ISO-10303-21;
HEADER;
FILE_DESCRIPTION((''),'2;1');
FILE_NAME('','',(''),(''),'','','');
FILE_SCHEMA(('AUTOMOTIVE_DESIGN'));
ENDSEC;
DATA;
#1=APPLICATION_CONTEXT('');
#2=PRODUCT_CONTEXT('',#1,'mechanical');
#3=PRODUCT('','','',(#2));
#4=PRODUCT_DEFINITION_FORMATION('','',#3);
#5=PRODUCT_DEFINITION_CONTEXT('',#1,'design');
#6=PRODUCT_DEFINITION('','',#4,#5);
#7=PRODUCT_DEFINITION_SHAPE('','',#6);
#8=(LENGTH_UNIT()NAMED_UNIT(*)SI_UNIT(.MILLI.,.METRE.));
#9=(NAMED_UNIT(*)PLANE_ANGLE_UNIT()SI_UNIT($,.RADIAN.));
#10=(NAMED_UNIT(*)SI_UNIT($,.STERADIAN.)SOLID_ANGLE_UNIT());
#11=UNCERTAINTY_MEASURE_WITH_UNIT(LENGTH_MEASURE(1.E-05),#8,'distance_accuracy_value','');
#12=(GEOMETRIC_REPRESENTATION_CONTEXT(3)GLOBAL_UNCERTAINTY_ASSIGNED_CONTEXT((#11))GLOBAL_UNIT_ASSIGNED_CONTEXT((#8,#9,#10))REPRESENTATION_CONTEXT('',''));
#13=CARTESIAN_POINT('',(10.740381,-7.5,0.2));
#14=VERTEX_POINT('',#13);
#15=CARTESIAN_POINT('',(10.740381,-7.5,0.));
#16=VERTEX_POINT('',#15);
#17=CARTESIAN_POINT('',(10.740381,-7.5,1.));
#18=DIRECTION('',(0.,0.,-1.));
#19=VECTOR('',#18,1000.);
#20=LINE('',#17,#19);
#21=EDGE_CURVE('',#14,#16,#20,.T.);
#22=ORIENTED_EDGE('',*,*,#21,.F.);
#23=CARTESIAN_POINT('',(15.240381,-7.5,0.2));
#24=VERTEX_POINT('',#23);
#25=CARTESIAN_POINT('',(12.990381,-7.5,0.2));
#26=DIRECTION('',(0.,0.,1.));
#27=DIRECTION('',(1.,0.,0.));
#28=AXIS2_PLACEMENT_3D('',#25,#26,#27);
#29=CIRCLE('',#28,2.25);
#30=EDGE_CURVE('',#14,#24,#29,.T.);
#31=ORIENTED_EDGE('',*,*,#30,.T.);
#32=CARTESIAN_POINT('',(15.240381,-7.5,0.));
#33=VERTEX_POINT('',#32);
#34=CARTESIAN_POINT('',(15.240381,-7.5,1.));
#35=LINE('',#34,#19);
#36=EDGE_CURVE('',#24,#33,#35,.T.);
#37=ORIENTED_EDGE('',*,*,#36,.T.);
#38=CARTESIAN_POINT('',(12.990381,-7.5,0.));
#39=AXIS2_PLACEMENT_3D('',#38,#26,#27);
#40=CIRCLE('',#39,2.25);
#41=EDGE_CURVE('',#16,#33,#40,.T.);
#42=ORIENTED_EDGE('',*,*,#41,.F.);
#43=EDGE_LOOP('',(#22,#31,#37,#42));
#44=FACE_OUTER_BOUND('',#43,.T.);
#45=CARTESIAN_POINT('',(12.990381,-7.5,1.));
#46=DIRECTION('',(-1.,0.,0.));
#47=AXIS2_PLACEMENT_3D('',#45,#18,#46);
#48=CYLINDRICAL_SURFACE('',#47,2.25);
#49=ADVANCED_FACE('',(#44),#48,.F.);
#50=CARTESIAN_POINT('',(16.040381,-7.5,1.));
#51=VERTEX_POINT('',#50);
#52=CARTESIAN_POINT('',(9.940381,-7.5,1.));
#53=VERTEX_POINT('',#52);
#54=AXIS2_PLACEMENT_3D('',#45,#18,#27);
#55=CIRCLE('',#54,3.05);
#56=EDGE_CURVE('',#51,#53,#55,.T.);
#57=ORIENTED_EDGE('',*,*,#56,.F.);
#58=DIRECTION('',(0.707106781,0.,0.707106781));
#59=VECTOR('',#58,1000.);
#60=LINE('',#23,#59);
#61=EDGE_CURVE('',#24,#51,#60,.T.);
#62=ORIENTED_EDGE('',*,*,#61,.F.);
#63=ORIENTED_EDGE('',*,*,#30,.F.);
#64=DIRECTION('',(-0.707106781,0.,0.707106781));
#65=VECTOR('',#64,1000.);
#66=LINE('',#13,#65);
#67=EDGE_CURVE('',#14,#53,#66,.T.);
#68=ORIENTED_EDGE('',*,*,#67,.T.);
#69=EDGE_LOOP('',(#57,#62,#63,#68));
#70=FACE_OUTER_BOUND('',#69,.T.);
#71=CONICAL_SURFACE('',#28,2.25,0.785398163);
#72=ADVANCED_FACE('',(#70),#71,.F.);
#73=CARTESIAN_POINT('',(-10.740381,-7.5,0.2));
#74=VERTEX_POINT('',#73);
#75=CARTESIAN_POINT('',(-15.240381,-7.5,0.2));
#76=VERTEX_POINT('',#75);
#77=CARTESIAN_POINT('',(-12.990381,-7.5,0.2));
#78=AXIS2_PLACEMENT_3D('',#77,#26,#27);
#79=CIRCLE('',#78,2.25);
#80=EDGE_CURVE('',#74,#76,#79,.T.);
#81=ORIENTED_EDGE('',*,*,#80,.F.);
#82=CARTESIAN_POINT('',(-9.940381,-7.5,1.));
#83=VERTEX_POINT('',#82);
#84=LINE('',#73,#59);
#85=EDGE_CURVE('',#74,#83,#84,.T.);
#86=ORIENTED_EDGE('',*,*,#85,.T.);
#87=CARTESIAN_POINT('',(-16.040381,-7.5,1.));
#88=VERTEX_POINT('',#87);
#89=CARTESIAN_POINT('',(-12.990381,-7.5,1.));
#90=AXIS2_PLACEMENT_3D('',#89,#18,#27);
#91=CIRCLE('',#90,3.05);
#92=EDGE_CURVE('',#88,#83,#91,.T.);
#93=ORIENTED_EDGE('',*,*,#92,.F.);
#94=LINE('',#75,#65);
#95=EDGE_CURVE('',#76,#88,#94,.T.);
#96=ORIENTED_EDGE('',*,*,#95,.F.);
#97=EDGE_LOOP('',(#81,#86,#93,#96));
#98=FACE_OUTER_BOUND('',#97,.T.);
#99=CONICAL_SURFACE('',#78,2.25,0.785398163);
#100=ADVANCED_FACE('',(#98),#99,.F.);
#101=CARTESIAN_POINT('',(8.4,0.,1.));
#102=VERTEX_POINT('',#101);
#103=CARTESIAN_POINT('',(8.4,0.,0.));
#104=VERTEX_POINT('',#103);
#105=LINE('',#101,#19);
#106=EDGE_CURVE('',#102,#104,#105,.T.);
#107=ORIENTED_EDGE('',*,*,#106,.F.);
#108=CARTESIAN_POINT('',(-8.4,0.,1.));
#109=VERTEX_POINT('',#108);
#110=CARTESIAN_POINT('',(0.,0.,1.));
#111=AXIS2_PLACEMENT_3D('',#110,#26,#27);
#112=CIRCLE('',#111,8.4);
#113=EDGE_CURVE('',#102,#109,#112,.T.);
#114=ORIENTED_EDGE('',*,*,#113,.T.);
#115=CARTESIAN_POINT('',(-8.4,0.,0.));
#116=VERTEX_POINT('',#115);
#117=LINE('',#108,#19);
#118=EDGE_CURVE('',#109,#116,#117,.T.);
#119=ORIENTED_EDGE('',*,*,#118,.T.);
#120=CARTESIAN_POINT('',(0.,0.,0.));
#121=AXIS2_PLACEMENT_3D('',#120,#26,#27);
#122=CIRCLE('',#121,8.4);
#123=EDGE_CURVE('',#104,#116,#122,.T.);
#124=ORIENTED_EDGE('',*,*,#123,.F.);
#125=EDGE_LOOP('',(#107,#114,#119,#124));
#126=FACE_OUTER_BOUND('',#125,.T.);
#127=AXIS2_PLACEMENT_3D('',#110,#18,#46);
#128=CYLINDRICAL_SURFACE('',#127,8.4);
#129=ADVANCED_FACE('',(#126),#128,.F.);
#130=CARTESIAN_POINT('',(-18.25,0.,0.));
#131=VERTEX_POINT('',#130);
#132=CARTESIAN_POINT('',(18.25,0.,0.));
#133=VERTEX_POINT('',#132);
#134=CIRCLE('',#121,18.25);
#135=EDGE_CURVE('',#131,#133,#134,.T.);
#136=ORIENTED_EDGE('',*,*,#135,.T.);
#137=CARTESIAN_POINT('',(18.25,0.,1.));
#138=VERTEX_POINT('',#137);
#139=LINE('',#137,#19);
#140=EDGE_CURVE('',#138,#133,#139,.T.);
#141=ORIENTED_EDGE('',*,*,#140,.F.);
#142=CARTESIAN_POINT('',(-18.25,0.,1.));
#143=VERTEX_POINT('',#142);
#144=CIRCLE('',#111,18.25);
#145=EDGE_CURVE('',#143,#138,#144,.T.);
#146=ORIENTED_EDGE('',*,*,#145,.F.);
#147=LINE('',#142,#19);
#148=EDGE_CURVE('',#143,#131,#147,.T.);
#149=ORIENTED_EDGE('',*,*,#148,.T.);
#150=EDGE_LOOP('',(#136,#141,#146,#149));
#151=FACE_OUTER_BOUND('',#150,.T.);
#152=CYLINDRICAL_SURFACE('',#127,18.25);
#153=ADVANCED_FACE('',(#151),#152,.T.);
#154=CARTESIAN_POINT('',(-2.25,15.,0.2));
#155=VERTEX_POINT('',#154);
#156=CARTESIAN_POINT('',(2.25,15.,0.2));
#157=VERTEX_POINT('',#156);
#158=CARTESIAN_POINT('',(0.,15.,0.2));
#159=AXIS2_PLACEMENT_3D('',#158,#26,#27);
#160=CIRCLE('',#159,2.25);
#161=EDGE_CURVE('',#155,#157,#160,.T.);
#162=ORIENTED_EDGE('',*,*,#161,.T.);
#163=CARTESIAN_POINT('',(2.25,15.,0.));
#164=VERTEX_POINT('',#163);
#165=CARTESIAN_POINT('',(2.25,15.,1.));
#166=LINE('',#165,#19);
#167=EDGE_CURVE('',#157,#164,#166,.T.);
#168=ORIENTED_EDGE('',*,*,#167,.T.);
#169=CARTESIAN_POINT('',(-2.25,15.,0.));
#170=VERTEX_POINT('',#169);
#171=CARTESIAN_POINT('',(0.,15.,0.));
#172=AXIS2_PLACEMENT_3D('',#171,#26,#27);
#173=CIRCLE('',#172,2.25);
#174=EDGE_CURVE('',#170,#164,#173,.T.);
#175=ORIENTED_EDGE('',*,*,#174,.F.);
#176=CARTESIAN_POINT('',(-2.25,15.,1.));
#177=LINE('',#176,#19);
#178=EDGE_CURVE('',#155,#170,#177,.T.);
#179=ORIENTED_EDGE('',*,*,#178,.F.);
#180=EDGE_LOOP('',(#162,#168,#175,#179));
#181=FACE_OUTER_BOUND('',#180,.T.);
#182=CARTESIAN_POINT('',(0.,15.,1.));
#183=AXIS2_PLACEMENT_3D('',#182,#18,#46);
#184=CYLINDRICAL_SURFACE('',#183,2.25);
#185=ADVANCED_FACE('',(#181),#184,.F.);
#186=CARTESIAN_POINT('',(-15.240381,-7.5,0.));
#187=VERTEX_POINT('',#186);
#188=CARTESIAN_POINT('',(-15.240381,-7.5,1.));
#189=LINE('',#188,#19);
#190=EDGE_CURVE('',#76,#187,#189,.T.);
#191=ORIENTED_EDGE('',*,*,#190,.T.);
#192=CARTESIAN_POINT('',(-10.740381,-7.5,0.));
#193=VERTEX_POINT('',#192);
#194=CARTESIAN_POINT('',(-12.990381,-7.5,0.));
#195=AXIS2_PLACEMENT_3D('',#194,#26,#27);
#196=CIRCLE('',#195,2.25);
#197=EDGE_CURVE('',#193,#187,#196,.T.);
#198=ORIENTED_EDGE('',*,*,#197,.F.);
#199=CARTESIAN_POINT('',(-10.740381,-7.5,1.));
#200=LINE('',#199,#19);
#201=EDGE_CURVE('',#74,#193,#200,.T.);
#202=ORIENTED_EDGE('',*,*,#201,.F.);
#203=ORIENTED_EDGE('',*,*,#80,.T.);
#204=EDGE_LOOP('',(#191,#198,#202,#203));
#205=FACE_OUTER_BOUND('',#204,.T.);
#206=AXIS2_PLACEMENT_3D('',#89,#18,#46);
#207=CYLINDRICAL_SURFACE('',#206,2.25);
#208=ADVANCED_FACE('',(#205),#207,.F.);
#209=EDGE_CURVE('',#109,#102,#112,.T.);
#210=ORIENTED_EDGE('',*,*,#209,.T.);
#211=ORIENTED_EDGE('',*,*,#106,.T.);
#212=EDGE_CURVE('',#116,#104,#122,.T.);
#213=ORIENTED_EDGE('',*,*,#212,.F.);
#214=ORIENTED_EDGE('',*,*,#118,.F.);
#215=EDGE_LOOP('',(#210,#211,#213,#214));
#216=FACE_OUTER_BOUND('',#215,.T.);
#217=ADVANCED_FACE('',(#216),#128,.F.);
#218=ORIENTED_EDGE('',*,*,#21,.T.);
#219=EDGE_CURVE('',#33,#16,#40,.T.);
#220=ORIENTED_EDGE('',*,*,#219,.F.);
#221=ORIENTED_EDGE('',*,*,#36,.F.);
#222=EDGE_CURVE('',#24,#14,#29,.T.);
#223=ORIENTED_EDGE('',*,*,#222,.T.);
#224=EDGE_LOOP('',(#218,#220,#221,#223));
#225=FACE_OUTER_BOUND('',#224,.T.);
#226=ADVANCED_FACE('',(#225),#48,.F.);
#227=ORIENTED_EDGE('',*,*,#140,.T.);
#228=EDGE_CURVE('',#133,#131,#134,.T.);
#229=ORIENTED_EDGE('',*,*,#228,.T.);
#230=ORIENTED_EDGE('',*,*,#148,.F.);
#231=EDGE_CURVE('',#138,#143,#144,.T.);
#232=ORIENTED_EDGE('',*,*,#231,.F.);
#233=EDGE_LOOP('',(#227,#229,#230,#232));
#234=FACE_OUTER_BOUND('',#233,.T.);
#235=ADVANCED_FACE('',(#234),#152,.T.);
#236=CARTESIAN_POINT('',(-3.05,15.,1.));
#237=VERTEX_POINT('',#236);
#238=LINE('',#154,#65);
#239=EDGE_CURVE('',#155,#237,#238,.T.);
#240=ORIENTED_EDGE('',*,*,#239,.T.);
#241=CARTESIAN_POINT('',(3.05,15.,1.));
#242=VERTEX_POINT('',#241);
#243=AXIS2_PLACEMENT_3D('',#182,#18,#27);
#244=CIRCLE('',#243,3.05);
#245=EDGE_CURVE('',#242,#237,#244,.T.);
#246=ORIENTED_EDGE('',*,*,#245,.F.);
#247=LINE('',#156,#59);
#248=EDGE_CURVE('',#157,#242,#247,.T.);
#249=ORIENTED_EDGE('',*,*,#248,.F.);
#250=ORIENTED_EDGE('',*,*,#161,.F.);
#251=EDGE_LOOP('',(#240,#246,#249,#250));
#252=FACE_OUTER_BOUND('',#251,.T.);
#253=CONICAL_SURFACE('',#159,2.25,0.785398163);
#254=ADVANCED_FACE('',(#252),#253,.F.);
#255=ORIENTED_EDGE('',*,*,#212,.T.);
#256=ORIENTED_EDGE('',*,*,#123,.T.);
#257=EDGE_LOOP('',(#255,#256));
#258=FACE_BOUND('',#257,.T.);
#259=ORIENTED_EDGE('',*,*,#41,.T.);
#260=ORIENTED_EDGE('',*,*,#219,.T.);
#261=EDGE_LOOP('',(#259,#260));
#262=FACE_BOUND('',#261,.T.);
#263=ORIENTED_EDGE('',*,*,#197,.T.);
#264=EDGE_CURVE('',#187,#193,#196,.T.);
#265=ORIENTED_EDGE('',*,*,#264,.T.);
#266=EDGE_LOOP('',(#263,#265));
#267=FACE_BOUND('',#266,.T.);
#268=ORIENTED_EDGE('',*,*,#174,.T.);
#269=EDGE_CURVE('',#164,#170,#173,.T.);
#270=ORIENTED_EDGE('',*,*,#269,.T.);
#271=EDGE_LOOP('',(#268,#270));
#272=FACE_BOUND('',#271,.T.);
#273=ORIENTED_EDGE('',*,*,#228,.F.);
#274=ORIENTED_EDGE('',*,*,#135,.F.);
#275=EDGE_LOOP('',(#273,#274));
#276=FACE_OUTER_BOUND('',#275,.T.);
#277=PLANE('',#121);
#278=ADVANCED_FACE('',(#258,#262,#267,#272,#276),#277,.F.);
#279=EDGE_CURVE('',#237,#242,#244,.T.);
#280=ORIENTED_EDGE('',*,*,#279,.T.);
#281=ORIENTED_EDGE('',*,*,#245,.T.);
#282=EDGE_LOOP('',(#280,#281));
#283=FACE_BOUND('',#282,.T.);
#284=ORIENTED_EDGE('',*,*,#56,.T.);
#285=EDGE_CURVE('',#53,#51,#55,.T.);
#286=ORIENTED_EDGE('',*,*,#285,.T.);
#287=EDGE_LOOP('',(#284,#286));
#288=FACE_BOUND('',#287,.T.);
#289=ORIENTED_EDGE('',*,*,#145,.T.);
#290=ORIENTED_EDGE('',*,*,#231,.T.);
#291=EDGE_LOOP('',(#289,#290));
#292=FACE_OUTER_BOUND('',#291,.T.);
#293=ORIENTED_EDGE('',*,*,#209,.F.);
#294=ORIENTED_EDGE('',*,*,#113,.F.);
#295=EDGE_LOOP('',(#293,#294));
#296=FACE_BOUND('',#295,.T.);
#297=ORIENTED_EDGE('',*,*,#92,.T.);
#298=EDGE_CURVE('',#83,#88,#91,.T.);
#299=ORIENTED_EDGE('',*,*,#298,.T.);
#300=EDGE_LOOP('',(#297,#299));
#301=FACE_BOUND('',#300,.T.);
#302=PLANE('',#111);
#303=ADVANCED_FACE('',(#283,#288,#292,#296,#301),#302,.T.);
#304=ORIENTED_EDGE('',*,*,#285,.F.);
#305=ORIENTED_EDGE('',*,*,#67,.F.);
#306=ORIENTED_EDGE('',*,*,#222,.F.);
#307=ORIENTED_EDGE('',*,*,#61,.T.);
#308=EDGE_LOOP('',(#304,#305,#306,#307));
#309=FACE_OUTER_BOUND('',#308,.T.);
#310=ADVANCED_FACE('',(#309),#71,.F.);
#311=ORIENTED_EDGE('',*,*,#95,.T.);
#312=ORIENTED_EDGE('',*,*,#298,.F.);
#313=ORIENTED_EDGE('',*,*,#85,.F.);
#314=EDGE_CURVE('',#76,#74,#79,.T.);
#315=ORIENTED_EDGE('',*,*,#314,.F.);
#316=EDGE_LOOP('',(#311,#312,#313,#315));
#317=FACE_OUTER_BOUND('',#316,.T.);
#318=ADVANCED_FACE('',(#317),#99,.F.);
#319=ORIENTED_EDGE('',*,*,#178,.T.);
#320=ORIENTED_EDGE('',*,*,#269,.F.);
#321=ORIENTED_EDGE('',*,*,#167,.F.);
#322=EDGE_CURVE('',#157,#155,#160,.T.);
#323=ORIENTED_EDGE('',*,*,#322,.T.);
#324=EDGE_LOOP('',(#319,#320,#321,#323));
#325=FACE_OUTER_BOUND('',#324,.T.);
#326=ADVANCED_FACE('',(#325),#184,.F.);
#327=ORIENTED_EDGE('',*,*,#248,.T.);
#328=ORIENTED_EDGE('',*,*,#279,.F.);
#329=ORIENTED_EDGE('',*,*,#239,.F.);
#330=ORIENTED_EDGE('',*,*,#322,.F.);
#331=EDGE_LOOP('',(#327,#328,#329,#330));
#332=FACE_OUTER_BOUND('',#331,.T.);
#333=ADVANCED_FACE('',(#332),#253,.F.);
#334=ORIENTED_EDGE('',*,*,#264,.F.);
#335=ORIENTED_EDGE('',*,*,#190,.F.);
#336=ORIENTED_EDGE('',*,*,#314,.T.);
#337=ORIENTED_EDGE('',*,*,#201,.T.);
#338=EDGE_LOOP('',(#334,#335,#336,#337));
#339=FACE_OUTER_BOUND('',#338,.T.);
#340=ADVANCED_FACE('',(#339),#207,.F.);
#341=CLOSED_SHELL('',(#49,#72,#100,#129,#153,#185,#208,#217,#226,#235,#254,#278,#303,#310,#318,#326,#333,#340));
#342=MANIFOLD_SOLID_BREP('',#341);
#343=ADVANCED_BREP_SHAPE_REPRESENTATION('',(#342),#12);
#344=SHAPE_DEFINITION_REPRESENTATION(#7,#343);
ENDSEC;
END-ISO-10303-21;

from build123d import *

# Parameters (mm, degrees)
SKETCH_1_R      = 18.25
SKETCH_1_R_2    = 8.4
SKETCH_1_R_3    = 2.25
EXTRUDE_1_DEPTH = 1
CHAMFER_1_SIZE  = 0.8


with BuildPart() as part:
    # 草图1 → 凸台-拉伸1 (new body)
    with BuildSketch(Plane.XY):
        Circle(SKETCH_1_R)
        Circle(SKETCH_1_R_2, mode=Mode.SUBTRACT)
        with Locations((0, 15)):
            Circle(SKETCH_1_R_3, mode=Mode.SUBTRACT)
        with Locations((12.990381057, -7.5)):
            Circle(SKETCH_1_R_3, mode=Mode.SUBTRACT)
        with Locations((-12.990381057, -7.5)):
            Circle(SKETCH_1_R_3, mode=Mode.SUBTRACT)
    extrude(amount=EXTRUDE_1_DEPTH)

    # 倒角1
    chamfer_1_edges = [part.edges().sort_by_distance(p)[0] for p in [
        (10.740381057, -7.5, 1),
        (-15.240381057, -7.5, 1),
        (-2.25, 15, 1),
    ]]
    chamfer(chamfer_1_edges, length=CHAMFER_1_SIZE)


solid = part.part
